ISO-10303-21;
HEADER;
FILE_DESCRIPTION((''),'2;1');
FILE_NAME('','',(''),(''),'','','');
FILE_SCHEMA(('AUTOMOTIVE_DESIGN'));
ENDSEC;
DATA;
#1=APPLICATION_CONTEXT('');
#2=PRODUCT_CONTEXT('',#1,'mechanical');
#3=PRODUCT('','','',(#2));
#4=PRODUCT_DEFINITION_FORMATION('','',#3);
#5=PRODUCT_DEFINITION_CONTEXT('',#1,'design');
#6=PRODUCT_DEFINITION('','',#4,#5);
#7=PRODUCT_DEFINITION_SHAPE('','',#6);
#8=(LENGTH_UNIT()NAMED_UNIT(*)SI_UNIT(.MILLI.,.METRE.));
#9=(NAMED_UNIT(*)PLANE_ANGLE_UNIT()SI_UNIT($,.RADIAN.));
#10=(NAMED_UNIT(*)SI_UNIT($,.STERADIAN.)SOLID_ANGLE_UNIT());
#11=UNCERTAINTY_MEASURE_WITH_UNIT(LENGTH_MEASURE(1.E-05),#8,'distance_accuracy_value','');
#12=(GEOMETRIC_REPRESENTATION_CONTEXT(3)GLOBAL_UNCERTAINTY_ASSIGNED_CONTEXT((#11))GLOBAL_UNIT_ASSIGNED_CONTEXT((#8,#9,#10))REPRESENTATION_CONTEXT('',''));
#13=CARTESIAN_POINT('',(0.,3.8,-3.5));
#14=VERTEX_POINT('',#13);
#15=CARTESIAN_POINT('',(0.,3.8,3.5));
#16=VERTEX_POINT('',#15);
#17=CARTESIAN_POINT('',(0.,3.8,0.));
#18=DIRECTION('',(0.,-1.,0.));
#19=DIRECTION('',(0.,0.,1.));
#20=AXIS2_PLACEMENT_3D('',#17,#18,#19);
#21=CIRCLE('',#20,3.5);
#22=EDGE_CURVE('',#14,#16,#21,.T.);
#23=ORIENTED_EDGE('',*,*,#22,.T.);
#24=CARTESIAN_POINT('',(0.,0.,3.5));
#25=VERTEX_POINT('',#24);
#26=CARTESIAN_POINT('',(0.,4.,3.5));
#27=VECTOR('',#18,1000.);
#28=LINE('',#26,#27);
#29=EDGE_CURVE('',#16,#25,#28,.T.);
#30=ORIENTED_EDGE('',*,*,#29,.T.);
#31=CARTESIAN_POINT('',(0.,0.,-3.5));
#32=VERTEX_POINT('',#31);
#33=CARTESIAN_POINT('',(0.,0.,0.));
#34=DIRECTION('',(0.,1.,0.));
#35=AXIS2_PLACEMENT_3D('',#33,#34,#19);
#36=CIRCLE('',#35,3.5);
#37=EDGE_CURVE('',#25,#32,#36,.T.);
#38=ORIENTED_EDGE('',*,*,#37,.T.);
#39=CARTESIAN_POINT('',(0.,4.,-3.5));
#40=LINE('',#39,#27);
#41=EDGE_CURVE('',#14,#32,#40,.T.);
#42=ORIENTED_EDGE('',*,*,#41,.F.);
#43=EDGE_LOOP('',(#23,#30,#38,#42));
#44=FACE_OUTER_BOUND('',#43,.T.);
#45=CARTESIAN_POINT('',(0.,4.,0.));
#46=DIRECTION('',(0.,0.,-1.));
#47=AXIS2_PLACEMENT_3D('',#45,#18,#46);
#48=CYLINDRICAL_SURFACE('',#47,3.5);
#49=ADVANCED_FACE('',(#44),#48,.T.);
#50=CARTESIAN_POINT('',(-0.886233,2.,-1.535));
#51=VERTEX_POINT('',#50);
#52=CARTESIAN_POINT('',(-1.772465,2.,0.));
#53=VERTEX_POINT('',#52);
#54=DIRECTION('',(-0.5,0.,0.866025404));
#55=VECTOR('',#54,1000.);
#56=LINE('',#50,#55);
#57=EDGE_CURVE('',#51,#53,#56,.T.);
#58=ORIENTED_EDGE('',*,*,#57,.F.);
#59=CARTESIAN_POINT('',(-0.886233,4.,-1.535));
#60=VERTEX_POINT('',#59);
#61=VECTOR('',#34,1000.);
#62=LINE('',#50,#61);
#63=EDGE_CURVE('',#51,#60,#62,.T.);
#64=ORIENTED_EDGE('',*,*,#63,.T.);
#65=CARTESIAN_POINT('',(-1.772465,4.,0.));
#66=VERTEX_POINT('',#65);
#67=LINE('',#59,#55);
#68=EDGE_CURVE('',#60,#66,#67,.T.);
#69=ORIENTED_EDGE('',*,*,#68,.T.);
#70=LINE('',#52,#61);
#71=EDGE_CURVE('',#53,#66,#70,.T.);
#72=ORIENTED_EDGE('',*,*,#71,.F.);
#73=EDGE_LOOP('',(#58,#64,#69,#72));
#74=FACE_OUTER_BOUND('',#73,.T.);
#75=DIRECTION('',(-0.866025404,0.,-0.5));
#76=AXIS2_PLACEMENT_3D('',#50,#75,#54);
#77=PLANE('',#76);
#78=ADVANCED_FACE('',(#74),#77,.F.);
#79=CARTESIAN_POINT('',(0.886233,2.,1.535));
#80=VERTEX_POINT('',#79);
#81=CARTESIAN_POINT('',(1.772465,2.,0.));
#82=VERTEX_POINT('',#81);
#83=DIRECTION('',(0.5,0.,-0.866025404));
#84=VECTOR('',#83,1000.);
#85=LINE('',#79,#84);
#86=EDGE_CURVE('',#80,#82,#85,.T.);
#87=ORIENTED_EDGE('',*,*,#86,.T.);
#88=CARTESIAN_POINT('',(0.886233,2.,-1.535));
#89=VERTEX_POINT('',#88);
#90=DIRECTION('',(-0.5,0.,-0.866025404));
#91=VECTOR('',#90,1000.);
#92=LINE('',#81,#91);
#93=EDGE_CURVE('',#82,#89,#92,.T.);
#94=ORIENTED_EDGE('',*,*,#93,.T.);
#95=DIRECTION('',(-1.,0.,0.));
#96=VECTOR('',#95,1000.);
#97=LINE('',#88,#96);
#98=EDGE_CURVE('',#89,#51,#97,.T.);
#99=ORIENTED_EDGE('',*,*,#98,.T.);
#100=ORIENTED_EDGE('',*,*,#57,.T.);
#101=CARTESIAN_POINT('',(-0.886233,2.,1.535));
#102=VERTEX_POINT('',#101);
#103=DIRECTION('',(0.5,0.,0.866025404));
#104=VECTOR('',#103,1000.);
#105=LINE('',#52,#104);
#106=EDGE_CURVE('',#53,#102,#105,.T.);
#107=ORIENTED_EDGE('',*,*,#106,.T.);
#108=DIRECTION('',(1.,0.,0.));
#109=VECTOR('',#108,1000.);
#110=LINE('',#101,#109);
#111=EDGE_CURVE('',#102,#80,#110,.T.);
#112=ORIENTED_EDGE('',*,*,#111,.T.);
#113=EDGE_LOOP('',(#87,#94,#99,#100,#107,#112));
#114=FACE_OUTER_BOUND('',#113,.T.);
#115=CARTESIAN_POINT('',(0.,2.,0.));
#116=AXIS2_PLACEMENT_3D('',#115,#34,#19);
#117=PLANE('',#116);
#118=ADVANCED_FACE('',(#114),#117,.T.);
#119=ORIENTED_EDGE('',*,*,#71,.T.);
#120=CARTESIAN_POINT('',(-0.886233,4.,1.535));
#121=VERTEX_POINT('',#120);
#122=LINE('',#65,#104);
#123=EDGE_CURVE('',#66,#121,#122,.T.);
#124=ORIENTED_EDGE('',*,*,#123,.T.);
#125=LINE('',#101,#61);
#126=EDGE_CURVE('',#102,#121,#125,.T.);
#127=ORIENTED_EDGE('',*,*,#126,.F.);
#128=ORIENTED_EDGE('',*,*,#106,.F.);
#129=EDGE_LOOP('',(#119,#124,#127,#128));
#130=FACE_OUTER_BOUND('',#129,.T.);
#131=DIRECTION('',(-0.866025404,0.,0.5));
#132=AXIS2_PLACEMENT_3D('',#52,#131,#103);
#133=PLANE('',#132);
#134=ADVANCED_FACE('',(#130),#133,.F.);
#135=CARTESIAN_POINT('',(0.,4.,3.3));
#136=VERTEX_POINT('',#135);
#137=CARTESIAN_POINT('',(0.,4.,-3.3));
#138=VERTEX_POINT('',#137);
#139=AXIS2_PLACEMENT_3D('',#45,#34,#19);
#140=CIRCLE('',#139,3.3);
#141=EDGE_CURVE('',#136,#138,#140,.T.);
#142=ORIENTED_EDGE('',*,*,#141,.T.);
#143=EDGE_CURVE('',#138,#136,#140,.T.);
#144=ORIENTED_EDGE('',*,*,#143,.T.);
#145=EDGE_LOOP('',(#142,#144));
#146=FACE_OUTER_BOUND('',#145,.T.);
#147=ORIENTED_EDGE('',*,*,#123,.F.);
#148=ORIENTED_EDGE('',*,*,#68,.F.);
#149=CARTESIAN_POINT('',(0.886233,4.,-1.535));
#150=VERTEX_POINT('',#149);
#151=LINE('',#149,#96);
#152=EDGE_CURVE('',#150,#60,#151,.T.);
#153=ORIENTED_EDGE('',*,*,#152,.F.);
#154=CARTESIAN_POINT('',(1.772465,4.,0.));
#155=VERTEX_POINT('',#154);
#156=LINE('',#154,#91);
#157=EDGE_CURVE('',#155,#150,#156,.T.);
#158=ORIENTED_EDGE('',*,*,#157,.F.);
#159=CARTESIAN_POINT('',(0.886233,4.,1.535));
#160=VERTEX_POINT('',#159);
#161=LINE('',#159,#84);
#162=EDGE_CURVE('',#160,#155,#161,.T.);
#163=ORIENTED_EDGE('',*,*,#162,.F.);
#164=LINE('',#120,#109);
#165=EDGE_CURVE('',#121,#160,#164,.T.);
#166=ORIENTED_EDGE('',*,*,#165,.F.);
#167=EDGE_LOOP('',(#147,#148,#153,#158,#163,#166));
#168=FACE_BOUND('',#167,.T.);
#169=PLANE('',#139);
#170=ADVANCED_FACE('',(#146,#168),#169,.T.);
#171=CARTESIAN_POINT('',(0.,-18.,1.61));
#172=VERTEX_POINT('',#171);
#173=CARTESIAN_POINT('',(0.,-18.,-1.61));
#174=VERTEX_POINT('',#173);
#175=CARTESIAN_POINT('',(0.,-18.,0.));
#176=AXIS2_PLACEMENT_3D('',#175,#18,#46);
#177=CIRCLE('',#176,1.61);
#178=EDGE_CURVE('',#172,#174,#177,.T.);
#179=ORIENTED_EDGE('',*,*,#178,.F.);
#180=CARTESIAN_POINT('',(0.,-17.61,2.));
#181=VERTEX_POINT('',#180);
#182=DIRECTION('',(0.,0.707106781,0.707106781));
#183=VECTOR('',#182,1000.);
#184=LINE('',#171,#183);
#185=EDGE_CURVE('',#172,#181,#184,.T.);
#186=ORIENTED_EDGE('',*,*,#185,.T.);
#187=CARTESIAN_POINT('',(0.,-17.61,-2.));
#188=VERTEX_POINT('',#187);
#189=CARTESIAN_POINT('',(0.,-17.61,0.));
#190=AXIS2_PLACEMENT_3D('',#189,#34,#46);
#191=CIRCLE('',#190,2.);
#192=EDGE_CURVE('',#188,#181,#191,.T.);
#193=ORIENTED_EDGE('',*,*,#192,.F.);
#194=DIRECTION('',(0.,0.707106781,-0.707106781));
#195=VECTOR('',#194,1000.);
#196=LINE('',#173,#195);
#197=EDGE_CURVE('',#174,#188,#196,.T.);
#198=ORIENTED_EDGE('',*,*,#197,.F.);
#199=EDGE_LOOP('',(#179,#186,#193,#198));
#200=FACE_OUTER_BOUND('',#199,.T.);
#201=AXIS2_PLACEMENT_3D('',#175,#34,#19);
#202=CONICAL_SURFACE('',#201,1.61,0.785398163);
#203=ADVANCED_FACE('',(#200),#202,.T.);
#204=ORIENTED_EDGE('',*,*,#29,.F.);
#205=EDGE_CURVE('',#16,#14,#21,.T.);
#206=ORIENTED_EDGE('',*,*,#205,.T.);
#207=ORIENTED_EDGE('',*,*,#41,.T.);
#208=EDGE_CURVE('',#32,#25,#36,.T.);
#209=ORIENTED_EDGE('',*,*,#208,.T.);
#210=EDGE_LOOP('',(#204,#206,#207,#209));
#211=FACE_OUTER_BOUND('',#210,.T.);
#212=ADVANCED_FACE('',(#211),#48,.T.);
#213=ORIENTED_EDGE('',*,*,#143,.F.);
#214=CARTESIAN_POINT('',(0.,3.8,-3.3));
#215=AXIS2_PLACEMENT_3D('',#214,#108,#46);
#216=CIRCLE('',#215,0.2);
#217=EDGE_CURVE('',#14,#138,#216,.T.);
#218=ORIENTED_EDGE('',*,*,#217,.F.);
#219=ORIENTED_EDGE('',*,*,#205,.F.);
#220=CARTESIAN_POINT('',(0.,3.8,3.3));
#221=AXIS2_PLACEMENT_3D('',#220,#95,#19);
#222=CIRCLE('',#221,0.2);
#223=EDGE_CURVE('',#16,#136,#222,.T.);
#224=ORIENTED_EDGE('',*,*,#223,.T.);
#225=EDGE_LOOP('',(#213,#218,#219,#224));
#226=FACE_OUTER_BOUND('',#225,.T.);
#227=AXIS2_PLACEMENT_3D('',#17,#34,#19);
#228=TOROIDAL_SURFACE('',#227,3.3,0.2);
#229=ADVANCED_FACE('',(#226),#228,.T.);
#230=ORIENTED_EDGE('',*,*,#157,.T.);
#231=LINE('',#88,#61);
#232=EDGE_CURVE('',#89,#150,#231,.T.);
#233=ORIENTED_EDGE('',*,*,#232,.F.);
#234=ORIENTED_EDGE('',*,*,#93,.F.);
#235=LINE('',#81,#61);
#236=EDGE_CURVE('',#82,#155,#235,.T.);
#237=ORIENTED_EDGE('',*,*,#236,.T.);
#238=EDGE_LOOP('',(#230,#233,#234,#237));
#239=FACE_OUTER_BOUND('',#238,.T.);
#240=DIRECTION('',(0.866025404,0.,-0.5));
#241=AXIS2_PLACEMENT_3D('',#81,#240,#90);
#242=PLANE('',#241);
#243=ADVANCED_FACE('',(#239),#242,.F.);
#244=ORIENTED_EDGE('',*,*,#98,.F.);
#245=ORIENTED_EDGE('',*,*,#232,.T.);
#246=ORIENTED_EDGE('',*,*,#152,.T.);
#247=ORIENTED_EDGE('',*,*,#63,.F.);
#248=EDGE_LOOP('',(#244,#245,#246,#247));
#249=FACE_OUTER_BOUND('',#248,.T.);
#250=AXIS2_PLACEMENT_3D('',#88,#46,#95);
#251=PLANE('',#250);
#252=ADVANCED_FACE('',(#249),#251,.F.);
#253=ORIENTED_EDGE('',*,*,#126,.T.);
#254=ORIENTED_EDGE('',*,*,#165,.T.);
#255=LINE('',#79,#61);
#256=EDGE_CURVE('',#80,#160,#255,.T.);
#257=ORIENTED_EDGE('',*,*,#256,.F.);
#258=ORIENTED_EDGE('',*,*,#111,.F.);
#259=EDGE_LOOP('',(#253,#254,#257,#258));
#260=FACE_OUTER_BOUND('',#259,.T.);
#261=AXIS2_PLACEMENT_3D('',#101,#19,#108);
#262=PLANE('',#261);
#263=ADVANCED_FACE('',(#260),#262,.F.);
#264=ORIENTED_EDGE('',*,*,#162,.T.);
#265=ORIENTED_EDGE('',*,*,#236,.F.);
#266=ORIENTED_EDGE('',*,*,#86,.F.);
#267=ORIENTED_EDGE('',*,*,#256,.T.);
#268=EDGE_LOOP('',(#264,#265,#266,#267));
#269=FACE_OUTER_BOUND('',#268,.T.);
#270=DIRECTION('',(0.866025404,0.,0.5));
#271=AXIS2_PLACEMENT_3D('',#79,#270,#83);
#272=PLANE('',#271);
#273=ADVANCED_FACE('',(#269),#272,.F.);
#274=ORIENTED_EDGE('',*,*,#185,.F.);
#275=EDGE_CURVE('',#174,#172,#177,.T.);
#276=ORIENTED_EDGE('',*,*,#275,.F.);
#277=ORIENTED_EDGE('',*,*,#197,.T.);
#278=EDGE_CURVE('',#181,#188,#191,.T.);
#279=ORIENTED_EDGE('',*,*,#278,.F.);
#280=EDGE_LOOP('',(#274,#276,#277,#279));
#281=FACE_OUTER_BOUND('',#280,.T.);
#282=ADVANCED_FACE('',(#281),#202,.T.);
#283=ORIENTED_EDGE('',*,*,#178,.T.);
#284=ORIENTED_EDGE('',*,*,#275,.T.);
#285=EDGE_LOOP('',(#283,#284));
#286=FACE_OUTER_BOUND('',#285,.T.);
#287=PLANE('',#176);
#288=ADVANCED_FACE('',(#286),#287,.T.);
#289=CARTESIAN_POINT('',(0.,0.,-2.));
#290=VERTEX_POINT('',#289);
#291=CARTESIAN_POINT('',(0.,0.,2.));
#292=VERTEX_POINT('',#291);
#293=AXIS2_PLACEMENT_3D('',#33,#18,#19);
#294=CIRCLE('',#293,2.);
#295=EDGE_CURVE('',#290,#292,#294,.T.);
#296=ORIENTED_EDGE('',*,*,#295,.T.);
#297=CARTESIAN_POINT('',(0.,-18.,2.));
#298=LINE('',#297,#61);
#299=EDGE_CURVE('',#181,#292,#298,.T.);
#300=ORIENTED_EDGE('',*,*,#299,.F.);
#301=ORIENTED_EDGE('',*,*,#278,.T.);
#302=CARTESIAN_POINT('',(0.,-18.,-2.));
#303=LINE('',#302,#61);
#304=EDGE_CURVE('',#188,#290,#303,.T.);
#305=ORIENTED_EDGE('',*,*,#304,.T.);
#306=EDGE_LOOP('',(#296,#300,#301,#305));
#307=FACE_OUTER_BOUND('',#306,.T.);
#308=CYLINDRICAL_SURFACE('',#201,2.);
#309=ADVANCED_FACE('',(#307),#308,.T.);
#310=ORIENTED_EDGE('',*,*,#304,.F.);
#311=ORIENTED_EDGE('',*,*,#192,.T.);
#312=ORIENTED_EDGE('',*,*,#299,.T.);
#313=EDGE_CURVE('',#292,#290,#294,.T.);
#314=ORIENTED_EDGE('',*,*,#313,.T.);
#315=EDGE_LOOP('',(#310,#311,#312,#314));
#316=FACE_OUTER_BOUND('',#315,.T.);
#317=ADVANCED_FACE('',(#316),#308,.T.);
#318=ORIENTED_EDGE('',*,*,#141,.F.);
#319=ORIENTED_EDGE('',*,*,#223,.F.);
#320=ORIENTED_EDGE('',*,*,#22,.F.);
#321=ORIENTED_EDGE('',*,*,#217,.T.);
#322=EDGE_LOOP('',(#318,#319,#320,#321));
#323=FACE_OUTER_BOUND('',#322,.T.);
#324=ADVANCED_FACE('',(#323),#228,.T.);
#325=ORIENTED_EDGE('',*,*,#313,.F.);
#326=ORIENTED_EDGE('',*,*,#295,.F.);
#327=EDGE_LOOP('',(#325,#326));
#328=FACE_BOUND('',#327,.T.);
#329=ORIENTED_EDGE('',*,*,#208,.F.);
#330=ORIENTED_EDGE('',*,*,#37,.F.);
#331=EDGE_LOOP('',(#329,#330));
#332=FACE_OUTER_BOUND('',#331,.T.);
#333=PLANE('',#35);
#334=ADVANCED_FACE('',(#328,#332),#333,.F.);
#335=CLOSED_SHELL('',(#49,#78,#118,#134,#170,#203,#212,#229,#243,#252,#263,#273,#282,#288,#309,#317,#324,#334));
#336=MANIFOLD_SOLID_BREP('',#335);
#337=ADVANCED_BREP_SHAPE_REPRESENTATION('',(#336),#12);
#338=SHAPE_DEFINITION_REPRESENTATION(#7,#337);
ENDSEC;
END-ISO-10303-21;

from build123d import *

# Parameters (mm, degrees)
SKETCH_1_R          = 3.5
EXTRUDE_1_DEPTH     = 4
CUT_EXTRUDE_1_DEPTH = 2
FILLET_1_R          = 0.2
SKETCH_5_R          = 2
EXTRUDE_2_DEPTH     = 18
CHAMFER_2_SIZE      = 0.39


with BuildPart() as part:
    # 草图1 → 凸台-拉伸1 (new body)
    with BuildSketch(Plane(origin=(0, 0, 0), x_dir=(1, 0, 0), z_dir=(0, 1, 0))):
        with Locations(Location((0, 0, 0), (0, 0, 270))):
            Circle(SKETCH_1_R)
    extrude(amount=EXTRUDE_1_DEPTH)

    # 草图2 → 切除-拉伸1 (cut)
    with BuildSketch(Plane(origin=(0, 4, 0), x_dir=(1, 0, 0), z_dir=(0, 1, 0))):
        Polygon((1.772465326, 0), (0.886232663, 1.535), (-0.886232663, 1.535), (-1.772465326, 0), (-0.886232663, -1.535), (0.886232663, -1.535), align=None)
    extrude(amount=-CUT_EXTRUDE_1_DEPTH, mode=Mode.SUBTRACT)

    # 圆角1
    fillet_1_edges = [part.edges().sort_by_distance(p)[0] for p in [
        (0, 4, -3.5),
    ]]
    fillet(fillet_1_edges, radius=FILLET_1_R)

    # 草图5 → 凸台-拉伸2 (add)
    with BuildSketch(Plane.XZ):
        with Locations(Location((0, 0, 0), (0, 0, 90))):
            Circle(SKETCH_5_R)
    extrude(amount=EXTRUDE_2_DEPTH)

    # 倒角2
    chamfer_2_edges = [part.edges().sort_by_distance(p)[0] for p in [
        (0, -18, -2),
    ]]
    chamfer(chamfer_2_edges, length=CHAMFER_2_SIZE)


solid = part.part
